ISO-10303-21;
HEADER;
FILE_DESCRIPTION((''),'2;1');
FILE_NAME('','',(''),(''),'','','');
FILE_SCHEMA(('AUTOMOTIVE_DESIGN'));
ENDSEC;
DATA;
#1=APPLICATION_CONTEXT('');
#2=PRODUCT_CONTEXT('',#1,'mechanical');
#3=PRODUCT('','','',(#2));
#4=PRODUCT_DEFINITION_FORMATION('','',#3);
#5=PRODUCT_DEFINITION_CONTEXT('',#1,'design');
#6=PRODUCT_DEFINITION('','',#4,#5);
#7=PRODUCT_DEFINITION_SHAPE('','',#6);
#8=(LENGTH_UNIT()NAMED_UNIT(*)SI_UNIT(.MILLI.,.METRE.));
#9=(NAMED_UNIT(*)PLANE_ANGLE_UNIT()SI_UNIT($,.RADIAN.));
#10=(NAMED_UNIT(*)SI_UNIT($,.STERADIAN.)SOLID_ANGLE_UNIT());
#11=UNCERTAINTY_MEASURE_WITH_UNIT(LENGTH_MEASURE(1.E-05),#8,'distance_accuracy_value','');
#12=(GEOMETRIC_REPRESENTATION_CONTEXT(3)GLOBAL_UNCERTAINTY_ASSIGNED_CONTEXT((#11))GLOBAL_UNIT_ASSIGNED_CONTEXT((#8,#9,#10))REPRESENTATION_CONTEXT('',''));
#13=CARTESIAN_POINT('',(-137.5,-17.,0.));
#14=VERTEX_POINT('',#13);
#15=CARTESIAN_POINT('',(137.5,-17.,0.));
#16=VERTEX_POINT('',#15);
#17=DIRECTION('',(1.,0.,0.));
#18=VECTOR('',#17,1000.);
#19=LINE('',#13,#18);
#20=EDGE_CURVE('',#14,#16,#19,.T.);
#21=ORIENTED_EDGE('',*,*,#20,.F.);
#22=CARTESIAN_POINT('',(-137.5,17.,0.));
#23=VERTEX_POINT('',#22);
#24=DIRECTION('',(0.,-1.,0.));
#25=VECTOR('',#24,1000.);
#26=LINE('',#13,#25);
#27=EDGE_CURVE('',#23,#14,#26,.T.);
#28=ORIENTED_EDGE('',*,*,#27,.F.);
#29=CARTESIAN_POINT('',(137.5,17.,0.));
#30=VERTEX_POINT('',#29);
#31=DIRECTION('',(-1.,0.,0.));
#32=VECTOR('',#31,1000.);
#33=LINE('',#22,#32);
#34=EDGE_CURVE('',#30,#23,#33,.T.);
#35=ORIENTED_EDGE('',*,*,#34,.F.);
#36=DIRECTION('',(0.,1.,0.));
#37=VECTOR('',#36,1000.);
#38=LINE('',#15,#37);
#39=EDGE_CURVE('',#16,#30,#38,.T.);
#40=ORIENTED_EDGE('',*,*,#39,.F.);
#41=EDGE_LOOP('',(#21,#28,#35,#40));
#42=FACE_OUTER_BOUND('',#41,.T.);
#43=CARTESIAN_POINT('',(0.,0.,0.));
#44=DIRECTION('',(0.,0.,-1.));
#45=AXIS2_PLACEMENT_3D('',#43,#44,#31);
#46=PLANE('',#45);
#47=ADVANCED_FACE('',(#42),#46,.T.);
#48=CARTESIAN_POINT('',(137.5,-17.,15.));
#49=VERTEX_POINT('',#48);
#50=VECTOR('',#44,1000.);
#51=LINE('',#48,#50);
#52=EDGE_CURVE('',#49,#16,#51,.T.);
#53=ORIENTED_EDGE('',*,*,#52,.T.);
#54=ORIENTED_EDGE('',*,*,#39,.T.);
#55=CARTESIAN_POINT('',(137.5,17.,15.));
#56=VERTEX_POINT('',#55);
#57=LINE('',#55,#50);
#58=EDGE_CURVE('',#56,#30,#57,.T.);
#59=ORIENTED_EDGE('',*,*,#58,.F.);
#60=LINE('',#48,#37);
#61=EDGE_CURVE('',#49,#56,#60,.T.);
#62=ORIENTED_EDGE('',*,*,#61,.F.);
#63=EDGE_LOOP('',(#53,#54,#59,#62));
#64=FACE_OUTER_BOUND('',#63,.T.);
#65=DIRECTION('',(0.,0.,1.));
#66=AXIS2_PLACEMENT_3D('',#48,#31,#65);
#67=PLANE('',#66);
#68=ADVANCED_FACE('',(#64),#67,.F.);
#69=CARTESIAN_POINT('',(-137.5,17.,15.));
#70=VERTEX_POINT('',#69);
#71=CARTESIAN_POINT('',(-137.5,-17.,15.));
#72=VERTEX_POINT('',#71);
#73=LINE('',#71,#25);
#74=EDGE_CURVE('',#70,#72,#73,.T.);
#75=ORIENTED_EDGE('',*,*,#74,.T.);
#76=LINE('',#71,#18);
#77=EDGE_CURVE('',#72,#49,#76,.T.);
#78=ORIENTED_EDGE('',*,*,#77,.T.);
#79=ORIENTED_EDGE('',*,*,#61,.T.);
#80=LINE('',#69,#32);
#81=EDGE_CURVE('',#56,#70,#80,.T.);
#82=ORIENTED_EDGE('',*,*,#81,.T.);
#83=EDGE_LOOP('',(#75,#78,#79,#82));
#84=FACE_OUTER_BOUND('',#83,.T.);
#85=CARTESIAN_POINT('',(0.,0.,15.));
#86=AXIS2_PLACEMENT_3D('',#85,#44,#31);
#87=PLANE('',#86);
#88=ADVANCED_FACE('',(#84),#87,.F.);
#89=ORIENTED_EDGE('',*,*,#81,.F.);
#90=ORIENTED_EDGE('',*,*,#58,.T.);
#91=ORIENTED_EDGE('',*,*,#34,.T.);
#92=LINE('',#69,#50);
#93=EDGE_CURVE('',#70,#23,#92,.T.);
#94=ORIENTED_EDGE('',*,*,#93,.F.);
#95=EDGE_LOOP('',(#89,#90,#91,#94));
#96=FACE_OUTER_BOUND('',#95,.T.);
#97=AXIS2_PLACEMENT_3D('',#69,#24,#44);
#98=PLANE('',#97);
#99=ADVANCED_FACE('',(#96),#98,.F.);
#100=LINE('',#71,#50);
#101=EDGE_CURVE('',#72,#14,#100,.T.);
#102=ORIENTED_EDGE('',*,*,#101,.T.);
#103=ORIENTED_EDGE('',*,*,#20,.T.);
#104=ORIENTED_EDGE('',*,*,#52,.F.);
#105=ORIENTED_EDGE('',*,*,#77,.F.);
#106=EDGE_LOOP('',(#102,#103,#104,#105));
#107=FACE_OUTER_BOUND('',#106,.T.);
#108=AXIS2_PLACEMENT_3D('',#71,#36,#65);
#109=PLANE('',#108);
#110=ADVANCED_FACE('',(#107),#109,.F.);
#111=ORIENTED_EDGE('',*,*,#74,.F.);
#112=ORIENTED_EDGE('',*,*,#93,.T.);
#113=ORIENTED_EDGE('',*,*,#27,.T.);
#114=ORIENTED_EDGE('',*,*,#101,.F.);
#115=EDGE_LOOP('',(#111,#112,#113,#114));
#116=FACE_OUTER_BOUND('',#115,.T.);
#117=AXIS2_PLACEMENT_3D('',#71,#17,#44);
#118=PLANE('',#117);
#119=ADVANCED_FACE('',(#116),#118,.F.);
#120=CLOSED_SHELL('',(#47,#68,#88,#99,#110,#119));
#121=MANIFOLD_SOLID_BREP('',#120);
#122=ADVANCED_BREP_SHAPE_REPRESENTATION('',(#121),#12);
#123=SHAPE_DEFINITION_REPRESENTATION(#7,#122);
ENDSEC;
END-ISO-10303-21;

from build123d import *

# Parameters (mm, degrees)
SKETCH_1_W      = 275
SKETCH_1_H      = 34
EXTRUDE_1_DEPTH = 15


with BuildPart() as part:
    # 草图1 → 凸台-拉伸1 (new body)
    with BuildSketch(Plane.XY):
        Rectangle(SKETCH_1_W, SKETCH_1_H)
    extrude(amount=EXTRUDE_1_DEPTH)


solid = part.part
